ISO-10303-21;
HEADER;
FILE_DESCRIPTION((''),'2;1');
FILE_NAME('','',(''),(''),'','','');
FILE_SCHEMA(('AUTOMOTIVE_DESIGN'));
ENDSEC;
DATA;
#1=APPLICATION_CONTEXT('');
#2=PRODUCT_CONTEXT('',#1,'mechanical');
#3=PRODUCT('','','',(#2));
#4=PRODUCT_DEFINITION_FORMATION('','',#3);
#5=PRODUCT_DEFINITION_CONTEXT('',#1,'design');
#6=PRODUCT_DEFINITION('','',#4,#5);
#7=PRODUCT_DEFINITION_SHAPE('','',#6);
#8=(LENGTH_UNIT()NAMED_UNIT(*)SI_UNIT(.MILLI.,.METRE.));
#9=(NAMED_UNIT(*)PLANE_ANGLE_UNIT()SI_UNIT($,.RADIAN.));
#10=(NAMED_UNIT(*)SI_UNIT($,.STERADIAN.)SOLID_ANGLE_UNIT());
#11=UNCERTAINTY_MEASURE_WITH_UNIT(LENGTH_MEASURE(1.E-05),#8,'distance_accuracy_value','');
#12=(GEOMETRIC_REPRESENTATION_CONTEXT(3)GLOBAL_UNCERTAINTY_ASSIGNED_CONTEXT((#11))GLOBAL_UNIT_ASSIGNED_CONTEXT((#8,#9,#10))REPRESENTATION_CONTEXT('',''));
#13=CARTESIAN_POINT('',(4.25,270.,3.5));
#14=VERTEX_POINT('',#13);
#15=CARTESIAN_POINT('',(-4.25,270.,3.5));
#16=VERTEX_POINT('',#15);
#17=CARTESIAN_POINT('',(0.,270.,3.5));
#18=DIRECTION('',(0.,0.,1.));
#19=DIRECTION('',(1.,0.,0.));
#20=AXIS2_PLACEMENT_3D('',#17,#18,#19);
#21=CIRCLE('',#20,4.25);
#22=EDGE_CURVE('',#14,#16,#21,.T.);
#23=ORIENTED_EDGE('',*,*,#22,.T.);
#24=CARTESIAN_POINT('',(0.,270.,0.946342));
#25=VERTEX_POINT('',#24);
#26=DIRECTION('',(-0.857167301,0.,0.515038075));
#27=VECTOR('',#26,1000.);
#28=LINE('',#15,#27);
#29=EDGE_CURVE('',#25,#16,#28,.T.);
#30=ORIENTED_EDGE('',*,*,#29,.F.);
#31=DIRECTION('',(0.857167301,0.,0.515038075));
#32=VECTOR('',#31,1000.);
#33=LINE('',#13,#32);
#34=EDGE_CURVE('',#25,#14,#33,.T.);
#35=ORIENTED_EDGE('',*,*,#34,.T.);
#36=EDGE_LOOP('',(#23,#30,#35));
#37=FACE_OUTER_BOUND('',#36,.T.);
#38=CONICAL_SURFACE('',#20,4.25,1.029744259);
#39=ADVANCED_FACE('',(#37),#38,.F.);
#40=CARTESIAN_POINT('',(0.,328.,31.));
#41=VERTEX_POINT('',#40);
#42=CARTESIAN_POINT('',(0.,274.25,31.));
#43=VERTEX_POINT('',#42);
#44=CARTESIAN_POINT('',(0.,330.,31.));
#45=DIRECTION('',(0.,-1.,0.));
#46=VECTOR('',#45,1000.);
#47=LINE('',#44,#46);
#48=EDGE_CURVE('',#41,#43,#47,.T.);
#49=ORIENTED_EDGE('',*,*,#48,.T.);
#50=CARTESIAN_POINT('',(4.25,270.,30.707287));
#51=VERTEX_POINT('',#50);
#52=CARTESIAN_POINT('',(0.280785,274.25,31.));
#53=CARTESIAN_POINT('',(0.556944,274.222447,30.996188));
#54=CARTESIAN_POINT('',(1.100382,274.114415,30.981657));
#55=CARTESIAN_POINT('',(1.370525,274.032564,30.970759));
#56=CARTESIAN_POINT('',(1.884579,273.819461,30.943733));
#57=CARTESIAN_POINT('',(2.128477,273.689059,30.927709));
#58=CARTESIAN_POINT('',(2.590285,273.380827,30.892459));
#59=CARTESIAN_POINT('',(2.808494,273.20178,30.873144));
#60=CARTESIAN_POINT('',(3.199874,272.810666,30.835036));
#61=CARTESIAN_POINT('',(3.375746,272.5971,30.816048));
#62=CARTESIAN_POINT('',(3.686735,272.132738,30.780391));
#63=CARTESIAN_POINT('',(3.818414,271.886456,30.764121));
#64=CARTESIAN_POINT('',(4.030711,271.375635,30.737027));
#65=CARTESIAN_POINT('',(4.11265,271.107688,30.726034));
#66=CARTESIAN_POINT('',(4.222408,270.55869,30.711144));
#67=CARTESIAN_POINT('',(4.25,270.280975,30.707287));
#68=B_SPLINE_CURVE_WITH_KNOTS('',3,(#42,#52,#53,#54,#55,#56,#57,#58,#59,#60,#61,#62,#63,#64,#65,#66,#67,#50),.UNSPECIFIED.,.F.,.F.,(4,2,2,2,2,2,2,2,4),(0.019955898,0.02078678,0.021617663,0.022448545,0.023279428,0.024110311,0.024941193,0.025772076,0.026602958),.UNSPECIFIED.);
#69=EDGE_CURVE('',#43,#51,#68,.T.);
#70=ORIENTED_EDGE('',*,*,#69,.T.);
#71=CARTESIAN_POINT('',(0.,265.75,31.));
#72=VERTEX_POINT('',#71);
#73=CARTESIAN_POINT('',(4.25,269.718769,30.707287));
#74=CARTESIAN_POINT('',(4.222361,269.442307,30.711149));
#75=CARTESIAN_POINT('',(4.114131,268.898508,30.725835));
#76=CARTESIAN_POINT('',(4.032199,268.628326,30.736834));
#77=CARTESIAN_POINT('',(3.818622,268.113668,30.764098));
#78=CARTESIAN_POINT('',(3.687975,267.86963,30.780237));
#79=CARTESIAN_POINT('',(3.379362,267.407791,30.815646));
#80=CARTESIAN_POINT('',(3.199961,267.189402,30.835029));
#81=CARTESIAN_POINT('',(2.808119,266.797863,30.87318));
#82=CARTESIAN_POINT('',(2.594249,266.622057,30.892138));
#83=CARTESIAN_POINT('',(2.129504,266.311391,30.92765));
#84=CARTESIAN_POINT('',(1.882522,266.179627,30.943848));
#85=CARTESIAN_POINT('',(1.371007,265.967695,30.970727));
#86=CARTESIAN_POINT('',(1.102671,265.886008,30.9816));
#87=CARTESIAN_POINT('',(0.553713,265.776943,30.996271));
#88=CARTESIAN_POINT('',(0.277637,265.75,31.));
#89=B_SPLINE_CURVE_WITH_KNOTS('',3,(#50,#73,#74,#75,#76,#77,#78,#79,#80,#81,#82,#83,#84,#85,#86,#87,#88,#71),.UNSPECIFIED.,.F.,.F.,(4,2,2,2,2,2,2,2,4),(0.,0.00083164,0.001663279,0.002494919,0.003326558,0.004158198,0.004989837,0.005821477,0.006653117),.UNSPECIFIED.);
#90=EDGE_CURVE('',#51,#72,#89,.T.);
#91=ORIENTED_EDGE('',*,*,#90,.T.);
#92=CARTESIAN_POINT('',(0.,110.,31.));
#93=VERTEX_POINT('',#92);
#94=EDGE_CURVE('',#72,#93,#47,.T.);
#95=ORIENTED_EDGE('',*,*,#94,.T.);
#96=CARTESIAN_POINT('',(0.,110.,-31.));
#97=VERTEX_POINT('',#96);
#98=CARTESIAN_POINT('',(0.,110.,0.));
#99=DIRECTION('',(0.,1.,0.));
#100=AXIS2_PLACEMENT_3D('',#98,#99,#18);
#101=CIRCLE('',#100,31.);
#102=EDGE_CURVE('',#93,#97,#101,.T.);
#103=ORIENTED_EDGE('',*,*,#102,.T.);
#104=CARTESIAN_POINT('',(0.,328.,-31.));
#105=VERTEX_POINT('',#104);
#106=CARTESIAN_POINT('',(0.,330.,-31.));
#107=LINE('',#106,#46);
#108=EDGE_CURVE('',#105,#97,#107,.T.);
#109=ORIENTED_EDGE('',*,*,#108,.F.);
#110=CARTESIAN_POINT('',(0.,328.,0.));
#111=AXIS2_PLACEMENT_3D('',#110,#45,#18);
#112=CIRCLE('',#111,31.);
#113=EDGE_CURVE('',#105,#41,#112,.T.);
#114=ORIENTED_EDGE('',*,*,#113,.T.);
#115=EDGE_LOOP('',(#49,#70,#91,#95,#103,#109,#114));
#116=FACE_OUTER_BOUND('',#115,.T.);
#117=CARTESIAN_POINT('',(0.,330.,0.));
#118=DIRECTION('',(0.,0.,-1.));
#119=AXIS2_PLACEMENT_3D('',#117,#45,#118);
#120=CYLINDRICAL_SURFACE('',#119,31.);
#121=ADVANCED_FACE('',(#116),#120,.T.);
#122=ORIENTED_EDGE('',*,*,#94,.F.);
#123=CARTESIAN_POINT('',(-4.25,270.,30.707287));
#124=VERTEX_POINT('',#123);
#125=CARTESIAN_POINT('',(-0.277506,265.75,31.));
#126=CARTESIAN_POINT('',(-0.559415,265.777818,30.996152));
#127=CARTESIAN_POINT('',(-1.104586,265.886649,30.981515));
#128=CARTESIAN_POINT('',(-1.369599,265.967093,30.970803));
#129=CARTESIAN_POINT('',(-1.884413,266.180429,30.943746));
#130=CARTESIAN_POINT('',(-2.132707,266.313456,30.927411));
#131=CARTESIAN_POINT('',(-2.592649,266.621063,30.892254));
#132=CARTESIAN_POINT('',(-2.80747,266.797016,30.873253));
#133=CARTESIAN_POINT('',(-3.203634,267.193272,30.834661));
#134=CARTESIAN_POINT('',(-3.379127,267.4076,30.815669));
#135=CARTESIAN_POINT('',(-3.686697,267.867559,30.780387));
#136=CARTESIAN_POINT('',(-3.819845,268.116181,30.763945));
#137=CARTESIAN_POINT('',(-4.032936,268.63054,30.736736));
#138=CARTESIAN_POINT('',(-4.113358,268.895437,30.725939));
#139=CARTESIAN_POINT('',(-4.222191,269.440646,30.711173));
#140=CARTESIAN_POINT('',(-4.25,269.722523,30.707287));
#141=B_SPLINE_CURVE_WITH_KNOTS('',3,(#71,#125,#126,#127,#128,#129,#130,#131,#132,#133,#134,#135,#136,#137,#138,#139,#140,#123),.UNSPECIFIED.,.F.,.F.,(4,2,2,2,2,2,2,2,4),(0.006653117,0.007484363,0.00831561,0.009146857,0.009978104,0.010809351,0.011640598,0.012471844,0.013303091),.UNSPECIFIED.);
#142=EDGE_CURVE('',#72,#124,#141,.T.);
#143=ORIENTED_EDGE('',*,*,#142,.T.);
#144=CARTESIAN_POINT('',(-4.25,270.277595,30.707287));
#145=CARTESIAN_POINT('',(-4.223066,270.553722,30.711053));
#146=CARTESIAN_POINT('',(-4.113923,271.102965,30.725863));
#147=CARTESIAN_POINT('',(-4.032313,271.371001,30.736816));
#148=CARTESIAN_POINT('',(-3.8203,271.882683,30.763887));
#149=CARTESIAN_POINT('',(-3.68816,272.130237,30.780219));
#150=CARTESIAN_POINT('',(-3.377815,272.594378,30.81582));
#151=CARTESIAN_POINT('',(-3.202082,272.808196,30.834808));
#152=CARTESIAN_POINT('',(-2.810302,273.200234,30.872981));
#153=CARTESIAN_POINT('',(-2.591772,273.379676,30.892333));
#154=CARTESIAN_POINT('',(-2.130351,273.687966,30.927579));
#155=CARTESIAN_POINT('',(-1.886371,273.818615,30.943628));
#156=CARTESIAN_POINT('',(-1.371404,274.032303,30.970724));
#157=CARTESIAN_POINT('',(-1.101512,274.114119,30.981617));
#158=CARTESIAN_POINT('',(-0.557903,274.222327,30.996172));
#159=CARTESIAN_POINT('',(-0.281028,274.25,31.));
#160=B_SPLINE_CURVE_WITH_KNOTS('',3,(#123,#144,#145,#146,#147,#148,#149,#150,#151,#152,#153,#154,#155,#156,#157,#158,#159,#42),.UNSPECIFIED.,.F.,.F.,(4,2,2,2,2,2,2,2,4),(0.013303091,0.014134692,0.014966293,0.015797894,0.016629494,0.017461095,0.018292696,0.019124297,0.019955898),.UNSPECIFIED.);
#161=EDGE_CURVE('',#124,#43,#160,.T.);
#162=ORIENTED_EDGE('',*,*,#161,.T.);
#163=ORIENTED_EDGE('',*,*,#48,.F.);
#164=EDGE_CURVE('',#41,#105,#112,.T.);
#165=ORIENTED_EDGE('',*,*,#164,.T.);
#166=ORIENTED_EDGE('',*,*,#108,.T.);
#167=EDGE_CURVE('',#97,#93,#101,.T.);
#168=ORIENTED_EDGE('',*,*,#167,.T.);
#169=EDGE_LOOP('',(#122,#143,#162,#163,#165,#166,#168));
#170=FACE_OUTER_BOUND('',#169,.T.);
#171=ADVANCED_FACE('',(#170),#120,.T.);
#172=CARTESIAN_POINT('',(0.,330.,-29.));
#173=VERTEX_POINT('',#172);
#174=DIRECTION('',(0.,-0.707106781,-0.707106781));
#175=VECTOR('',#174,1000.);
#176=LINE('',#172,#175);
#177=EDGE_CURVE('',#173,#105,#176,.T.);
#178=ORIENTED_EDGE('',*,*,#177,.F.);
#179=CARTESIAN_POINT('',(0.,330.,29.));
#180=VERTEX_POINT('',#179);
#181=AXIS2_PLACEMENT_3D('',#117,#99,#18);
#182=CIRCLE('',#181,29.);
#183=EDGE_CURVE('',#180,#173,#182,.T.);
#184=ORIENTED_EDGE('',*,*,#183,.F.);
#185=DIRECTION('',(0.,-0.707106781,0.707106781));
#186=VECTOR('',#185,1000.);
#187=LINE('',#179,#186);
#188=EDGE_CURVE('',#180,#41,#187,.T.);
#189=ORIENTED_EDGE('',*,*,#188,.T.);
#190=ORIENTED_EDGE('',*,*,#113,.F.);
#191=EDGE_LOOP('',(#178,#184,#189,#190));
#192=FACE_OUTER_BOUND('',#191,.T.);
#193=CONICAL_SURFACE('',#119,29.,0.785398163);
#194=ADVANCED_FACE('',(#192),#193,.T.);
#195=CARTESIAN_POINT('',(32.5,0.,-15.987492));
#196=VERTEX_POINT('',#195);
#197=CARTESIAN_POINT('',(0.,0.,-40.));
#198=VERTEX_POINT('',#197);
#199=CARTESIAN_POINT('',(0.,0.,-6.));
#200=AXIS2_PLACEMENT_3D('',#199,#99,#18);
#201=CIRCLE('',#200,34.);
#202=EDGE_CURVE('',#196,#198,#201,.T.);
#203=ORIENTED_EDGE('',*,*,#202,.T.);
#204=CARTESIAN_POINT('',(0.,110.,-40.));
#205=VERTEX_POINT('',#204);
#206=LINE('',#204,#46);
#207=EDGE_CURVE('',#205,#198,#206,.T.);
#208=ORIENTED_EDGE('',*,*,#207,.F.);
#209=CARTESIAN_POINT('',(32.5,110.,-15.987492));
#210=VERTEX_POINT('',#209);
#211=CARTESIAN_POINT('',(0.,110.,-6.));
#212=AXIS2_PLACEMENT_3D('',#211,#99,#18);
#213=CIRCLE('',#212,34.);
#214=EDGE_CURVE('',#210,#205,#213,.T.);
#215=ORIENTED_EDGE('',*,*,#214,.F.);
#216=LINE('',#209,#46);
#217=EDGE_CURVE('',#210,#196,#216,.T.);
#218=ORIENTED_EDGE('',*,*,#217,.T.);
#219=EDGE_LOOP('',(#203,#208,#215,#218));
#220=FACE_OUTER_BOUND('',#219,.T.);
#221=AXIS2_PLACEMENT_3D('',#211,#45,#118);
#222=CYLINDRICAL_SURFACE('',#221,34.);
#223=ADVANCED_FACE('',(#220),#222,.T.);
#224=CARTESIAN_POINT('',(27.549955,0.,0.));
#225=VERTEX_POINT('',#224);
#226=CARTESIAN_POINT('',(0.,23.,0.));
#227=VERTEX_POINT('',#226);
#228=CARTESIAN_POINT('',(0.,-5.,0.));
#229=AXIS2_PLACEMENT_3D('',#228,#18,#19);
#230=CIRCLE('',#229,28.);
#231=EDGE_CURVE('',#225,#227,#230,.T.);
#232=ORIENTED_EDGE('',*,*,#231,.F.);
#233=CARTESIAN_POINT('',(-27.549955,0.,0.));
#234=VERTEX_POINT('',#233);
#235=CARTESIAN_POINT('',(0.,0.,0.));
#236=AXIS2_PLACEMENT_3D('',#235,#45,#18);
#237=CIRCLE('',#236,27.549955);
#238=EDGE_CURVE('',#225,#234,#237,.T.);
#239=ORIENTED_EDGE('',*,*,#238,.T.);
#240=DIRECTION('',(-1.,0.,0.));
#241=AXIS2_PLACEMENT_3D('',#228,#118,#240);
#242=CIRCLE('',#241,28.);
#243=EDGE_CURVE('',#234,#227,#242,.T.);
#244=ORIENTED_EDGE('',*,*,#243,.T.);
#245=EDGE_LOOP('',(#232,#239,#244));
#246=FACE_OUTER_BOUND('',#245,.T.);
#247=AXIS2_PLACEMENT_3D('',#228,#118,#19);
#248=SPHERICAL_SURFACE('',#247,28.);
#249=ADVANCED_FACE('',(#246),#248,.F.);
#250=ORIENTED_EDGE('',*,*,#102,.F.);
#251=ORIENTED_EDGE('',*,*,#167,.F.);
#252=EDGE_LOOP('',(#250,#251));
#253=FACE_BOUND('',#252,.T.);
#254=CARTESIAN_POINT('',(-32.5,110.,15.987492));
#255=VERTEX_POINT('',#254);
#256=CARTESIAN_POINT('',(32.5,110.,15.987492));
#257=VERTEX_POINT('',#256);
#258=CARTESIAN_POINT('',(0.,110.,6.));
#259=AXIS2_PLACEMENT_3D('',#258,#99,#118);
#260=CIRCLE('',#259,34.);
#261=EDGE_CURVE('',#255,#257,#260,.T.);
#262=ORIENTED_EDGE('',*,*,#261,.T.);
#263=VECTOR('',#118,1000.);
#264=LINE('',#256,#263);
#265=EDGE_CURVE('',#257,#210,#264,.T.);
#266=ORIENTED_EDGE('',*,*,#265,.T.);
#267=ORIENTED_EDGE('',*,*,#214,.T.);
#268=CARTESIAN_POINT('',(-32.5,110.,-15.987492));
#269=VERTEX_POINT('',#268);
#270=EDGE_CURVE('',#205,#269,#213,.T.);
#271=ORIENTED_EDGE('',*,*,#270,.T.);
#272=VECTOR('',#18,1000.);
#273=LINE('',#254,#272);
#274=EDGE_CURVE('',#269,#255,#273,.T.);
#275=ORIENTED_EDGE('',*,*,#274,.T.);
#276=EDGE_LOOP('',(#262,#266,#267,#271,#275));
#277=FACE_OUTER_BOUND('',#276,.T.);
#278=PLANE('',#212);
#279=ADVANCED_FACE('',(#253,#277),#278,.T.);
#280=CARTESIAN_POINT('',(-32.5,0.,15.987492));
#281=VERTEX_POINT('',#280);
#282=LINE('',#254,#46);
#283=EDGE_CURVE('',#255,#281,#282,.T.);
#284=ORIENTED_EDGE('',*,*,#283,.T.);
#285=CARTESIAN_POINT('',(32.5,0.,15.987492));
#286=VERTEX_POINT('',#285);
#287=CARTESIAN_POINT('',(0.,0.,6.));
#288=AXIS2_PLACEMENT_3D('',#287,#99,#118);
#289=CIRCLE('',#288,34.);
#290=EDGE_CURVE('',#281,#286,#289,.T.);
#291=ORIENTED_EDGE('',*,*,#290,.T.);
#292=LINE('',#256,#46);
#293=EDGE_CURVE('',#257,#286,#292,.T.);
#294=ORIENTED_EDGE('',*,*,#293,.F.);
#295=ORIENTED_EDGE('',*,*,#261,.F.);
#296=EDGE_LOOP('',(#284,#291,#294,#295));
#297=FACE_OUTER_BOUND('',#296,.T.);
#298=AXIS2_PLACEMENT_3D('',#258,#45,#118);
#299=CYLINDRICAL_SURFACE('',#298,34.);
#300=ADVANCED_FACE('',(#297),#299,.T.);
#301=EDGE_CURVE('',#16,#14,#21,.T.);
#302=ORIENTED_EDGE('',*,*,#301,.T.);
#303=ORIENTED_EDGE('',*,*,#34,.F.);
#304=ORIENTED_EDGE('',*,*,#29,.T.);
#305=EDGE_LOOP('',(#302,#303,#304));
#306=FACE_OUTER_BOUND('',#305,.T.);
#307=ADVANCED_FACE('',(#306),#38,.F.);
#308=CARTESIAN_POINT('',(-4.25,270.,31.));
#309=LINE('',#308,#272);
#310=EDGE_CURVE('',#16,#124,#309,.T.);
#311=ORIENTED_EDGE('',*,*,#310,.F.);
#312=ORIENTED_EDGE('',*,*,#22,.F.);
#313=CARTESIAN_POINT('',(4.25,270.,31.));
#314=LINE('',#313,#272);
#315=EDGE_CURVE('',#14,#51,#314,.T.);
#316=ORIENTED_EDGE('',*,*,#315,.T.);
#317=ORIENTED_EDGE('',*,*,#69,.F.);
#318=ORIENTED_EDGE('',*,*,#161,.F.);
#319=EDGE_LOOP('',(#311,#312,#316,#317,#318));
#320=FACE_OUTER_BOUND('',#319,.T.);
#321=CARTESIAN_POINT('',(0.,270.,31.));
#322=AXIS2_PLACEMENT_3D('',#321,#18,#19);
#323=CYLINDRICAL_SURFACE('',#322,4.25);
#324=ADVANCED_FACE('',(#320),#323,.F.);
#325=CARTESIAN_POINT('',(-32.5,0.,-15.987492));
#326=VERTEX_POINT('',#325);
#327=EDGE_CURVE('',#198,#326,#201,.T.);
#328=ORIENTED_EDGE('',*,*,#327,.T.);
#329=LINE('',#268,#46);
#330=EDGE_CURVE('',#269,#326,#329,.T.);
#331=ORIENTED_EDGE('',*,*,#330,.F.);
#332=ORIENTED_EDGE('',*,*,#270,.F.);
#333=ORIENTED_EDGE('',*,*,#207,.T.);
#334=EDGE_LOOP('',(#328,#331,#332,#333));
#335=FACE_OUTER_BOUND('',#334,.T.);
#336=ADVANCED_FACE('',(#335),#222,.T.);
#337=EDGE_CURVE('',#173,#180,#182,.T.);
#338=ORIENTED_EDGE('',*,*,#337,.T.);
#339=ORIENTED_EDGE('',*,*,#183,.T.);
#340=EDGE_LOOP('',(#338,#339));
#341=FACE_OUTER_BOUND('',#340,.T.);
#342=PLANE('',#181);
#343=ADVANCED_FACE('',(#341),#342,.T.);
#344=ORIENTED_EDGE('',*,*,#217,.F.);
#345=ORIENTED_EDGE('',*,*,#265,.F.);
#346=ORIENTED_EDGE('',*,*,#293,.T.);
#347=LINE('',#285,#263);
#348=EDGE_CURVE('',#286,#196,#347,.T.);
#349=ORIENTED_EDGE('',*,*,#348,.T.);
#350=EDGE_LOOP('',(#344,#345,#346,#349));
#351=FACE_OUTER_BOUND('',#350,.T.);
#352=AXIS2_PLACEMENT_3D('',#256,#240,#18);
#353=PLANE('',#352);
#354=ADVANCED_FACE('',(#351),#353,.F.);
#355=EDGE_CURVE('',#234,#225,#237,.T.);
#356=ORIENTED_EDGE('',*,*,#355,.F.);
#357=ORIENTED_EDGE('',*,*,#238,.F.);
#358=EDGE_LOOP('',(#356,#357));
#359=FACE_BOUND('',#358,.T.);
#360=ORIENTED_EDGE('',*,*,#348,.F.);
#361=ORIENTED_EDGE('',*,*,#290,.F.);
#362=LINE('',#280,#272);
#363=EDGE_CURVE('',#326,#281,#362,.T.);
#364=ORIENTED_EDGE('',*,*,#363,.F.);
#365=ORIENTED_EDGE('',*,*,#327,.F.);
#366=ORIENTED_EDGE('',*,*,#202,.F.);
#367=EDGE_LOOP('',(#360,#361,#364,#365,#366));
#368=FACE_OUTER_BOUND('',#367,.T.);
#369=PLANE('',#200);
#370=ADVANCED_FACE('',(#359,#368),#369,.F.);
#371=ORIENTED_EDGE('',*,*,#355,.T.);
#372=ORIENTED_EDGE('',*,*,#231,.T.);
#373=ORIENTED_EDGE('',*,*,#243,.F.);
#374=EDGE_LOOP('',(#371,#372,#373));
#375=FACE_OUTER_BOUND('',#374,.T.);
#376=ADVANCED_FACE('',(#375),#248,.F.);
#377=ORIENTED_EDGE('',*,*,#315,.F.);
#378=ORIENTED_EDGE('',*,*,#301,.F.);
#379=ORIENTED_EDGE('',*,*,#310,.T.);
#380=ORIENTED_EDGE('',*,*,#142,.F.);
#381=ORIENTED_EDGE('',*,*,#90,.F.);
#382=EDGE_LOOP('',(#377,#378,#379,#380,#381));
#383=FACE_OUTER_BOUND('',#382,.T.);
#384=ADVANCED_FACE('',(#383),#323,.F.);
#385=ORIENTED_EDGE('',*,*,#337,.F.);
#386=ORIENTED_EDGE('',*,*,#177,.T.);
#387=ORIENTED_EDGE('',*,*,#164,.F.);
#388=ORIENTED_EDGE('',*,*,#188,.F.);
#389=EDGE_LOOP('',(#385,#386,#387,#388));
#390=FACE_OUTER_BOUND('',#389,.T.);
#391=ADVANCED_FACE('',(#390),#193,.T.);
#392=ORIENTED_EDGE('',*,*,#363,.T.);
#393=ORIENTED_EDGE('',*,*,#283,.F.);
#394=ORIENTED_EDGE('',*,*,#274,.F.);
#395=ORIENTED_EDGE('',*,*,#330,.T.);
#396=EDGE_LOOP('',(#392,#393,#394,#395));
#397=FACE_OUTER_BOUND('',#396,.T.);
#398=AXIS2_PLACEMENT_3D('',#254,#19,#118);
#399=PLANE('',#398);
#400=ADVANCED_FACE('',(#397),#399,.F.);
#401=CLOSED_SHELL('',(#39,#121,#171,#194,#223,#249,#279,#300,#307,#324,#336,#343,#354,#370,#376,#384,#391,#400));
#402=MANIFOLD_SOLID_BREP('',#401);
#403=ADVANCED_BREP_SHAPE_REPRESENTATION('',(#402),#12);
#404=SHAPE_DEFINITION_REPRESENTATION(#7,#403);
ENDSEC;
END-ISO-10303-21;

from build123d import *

# Parameters (mm, degrees)
EXTRUDE_1_DEPTH         = 110
SKETCH_2_R              = 31
EXTRUDE_2_DEPTH         = 220
HOLE_WIZARD_M10_1_D     = 8.5
HOLE_WIZARD_M10_1_DEPTH = 27.5
HOLE_WIZARD_M10_1_TIP   = 2.553657631
CHAMFER_1_SIZE          = 2


with BuildPart() as part:
    # 草图1 → 凸台-拉伸1 (new body)
    with BuildSketch(Plane(origin=(0, 0, 0), x_dir=(1, 0, 0), z_dir=(0, 1, 0))):
        with BuildLine():
            Line((32.5, -15.987492178), (32.5, 15.987492178))
            ThreePointArc((32.5, 15.987492178), (0, 40), (-32.5, 15.987492178))
            Line((-32.5, 15.987492178), (-32.5, -15.987492178))
            ThreePointArc((-32.5, -15.987492178), (0, -40), (32.5, -15.987492178))
        make_face()
    extrude(amount=EXTRUDE_1_DEPTH)

    # 草图2 → 凸台-拉伸2 (add)
    with BuildSketch(Plane(origin=(0, 110, 0), x_dir=(1, 0, 0), z_dir=(0, 1, 0))):
        with Locations(Location((0, 0, 0), (0, 0, 270))):
            Circle(SKETCH_2_R)
    extrude(amount=EXTRUDE_2_DEPTH)

    # M10 螺纹孔1
    with Locations(Plane.XY.offset(31)):
        with Locations((0, 270)):
            Hole(HOLE_WIZARD_M10_1_D / 2, depth=HOLE_WIZARD_M10_1_DEPTH)
            with Locations((0, 0, -(HOLE_WIZARD_M10_1_DEPTH + HOLE_WIZARD_M10_1_TIP / 2))):  # 118° drill point
                Cone(0, HOLE_WIZARD_M10_1_D / 2, HOLE_WIZARD_M10_1_TIP, mode=Mode.SUBTRACT)

    # 倒角1
    chamfer_1_edges = [part.edges().sort_by_distance(p)[0] for p in [
        (0, 330, -31),
    ]]
    chamfer(chamfer_1_edges, length=CHAMFER_1_SIZE)

    # 草图5 → 切除-旋转1 (revolve, cut)
    with BuildSketch(Plane.XY):
        with BuildLine():
            Line((0, 23), (0, -33))
            ThreePointArc((0, -33), (28, -5), (0, 23))
        make_face()
    revolve(axis=Axis((0, 23, 0), (0, -1, 0)), mode=Mode.SUBTRACT)


solid = part.part
